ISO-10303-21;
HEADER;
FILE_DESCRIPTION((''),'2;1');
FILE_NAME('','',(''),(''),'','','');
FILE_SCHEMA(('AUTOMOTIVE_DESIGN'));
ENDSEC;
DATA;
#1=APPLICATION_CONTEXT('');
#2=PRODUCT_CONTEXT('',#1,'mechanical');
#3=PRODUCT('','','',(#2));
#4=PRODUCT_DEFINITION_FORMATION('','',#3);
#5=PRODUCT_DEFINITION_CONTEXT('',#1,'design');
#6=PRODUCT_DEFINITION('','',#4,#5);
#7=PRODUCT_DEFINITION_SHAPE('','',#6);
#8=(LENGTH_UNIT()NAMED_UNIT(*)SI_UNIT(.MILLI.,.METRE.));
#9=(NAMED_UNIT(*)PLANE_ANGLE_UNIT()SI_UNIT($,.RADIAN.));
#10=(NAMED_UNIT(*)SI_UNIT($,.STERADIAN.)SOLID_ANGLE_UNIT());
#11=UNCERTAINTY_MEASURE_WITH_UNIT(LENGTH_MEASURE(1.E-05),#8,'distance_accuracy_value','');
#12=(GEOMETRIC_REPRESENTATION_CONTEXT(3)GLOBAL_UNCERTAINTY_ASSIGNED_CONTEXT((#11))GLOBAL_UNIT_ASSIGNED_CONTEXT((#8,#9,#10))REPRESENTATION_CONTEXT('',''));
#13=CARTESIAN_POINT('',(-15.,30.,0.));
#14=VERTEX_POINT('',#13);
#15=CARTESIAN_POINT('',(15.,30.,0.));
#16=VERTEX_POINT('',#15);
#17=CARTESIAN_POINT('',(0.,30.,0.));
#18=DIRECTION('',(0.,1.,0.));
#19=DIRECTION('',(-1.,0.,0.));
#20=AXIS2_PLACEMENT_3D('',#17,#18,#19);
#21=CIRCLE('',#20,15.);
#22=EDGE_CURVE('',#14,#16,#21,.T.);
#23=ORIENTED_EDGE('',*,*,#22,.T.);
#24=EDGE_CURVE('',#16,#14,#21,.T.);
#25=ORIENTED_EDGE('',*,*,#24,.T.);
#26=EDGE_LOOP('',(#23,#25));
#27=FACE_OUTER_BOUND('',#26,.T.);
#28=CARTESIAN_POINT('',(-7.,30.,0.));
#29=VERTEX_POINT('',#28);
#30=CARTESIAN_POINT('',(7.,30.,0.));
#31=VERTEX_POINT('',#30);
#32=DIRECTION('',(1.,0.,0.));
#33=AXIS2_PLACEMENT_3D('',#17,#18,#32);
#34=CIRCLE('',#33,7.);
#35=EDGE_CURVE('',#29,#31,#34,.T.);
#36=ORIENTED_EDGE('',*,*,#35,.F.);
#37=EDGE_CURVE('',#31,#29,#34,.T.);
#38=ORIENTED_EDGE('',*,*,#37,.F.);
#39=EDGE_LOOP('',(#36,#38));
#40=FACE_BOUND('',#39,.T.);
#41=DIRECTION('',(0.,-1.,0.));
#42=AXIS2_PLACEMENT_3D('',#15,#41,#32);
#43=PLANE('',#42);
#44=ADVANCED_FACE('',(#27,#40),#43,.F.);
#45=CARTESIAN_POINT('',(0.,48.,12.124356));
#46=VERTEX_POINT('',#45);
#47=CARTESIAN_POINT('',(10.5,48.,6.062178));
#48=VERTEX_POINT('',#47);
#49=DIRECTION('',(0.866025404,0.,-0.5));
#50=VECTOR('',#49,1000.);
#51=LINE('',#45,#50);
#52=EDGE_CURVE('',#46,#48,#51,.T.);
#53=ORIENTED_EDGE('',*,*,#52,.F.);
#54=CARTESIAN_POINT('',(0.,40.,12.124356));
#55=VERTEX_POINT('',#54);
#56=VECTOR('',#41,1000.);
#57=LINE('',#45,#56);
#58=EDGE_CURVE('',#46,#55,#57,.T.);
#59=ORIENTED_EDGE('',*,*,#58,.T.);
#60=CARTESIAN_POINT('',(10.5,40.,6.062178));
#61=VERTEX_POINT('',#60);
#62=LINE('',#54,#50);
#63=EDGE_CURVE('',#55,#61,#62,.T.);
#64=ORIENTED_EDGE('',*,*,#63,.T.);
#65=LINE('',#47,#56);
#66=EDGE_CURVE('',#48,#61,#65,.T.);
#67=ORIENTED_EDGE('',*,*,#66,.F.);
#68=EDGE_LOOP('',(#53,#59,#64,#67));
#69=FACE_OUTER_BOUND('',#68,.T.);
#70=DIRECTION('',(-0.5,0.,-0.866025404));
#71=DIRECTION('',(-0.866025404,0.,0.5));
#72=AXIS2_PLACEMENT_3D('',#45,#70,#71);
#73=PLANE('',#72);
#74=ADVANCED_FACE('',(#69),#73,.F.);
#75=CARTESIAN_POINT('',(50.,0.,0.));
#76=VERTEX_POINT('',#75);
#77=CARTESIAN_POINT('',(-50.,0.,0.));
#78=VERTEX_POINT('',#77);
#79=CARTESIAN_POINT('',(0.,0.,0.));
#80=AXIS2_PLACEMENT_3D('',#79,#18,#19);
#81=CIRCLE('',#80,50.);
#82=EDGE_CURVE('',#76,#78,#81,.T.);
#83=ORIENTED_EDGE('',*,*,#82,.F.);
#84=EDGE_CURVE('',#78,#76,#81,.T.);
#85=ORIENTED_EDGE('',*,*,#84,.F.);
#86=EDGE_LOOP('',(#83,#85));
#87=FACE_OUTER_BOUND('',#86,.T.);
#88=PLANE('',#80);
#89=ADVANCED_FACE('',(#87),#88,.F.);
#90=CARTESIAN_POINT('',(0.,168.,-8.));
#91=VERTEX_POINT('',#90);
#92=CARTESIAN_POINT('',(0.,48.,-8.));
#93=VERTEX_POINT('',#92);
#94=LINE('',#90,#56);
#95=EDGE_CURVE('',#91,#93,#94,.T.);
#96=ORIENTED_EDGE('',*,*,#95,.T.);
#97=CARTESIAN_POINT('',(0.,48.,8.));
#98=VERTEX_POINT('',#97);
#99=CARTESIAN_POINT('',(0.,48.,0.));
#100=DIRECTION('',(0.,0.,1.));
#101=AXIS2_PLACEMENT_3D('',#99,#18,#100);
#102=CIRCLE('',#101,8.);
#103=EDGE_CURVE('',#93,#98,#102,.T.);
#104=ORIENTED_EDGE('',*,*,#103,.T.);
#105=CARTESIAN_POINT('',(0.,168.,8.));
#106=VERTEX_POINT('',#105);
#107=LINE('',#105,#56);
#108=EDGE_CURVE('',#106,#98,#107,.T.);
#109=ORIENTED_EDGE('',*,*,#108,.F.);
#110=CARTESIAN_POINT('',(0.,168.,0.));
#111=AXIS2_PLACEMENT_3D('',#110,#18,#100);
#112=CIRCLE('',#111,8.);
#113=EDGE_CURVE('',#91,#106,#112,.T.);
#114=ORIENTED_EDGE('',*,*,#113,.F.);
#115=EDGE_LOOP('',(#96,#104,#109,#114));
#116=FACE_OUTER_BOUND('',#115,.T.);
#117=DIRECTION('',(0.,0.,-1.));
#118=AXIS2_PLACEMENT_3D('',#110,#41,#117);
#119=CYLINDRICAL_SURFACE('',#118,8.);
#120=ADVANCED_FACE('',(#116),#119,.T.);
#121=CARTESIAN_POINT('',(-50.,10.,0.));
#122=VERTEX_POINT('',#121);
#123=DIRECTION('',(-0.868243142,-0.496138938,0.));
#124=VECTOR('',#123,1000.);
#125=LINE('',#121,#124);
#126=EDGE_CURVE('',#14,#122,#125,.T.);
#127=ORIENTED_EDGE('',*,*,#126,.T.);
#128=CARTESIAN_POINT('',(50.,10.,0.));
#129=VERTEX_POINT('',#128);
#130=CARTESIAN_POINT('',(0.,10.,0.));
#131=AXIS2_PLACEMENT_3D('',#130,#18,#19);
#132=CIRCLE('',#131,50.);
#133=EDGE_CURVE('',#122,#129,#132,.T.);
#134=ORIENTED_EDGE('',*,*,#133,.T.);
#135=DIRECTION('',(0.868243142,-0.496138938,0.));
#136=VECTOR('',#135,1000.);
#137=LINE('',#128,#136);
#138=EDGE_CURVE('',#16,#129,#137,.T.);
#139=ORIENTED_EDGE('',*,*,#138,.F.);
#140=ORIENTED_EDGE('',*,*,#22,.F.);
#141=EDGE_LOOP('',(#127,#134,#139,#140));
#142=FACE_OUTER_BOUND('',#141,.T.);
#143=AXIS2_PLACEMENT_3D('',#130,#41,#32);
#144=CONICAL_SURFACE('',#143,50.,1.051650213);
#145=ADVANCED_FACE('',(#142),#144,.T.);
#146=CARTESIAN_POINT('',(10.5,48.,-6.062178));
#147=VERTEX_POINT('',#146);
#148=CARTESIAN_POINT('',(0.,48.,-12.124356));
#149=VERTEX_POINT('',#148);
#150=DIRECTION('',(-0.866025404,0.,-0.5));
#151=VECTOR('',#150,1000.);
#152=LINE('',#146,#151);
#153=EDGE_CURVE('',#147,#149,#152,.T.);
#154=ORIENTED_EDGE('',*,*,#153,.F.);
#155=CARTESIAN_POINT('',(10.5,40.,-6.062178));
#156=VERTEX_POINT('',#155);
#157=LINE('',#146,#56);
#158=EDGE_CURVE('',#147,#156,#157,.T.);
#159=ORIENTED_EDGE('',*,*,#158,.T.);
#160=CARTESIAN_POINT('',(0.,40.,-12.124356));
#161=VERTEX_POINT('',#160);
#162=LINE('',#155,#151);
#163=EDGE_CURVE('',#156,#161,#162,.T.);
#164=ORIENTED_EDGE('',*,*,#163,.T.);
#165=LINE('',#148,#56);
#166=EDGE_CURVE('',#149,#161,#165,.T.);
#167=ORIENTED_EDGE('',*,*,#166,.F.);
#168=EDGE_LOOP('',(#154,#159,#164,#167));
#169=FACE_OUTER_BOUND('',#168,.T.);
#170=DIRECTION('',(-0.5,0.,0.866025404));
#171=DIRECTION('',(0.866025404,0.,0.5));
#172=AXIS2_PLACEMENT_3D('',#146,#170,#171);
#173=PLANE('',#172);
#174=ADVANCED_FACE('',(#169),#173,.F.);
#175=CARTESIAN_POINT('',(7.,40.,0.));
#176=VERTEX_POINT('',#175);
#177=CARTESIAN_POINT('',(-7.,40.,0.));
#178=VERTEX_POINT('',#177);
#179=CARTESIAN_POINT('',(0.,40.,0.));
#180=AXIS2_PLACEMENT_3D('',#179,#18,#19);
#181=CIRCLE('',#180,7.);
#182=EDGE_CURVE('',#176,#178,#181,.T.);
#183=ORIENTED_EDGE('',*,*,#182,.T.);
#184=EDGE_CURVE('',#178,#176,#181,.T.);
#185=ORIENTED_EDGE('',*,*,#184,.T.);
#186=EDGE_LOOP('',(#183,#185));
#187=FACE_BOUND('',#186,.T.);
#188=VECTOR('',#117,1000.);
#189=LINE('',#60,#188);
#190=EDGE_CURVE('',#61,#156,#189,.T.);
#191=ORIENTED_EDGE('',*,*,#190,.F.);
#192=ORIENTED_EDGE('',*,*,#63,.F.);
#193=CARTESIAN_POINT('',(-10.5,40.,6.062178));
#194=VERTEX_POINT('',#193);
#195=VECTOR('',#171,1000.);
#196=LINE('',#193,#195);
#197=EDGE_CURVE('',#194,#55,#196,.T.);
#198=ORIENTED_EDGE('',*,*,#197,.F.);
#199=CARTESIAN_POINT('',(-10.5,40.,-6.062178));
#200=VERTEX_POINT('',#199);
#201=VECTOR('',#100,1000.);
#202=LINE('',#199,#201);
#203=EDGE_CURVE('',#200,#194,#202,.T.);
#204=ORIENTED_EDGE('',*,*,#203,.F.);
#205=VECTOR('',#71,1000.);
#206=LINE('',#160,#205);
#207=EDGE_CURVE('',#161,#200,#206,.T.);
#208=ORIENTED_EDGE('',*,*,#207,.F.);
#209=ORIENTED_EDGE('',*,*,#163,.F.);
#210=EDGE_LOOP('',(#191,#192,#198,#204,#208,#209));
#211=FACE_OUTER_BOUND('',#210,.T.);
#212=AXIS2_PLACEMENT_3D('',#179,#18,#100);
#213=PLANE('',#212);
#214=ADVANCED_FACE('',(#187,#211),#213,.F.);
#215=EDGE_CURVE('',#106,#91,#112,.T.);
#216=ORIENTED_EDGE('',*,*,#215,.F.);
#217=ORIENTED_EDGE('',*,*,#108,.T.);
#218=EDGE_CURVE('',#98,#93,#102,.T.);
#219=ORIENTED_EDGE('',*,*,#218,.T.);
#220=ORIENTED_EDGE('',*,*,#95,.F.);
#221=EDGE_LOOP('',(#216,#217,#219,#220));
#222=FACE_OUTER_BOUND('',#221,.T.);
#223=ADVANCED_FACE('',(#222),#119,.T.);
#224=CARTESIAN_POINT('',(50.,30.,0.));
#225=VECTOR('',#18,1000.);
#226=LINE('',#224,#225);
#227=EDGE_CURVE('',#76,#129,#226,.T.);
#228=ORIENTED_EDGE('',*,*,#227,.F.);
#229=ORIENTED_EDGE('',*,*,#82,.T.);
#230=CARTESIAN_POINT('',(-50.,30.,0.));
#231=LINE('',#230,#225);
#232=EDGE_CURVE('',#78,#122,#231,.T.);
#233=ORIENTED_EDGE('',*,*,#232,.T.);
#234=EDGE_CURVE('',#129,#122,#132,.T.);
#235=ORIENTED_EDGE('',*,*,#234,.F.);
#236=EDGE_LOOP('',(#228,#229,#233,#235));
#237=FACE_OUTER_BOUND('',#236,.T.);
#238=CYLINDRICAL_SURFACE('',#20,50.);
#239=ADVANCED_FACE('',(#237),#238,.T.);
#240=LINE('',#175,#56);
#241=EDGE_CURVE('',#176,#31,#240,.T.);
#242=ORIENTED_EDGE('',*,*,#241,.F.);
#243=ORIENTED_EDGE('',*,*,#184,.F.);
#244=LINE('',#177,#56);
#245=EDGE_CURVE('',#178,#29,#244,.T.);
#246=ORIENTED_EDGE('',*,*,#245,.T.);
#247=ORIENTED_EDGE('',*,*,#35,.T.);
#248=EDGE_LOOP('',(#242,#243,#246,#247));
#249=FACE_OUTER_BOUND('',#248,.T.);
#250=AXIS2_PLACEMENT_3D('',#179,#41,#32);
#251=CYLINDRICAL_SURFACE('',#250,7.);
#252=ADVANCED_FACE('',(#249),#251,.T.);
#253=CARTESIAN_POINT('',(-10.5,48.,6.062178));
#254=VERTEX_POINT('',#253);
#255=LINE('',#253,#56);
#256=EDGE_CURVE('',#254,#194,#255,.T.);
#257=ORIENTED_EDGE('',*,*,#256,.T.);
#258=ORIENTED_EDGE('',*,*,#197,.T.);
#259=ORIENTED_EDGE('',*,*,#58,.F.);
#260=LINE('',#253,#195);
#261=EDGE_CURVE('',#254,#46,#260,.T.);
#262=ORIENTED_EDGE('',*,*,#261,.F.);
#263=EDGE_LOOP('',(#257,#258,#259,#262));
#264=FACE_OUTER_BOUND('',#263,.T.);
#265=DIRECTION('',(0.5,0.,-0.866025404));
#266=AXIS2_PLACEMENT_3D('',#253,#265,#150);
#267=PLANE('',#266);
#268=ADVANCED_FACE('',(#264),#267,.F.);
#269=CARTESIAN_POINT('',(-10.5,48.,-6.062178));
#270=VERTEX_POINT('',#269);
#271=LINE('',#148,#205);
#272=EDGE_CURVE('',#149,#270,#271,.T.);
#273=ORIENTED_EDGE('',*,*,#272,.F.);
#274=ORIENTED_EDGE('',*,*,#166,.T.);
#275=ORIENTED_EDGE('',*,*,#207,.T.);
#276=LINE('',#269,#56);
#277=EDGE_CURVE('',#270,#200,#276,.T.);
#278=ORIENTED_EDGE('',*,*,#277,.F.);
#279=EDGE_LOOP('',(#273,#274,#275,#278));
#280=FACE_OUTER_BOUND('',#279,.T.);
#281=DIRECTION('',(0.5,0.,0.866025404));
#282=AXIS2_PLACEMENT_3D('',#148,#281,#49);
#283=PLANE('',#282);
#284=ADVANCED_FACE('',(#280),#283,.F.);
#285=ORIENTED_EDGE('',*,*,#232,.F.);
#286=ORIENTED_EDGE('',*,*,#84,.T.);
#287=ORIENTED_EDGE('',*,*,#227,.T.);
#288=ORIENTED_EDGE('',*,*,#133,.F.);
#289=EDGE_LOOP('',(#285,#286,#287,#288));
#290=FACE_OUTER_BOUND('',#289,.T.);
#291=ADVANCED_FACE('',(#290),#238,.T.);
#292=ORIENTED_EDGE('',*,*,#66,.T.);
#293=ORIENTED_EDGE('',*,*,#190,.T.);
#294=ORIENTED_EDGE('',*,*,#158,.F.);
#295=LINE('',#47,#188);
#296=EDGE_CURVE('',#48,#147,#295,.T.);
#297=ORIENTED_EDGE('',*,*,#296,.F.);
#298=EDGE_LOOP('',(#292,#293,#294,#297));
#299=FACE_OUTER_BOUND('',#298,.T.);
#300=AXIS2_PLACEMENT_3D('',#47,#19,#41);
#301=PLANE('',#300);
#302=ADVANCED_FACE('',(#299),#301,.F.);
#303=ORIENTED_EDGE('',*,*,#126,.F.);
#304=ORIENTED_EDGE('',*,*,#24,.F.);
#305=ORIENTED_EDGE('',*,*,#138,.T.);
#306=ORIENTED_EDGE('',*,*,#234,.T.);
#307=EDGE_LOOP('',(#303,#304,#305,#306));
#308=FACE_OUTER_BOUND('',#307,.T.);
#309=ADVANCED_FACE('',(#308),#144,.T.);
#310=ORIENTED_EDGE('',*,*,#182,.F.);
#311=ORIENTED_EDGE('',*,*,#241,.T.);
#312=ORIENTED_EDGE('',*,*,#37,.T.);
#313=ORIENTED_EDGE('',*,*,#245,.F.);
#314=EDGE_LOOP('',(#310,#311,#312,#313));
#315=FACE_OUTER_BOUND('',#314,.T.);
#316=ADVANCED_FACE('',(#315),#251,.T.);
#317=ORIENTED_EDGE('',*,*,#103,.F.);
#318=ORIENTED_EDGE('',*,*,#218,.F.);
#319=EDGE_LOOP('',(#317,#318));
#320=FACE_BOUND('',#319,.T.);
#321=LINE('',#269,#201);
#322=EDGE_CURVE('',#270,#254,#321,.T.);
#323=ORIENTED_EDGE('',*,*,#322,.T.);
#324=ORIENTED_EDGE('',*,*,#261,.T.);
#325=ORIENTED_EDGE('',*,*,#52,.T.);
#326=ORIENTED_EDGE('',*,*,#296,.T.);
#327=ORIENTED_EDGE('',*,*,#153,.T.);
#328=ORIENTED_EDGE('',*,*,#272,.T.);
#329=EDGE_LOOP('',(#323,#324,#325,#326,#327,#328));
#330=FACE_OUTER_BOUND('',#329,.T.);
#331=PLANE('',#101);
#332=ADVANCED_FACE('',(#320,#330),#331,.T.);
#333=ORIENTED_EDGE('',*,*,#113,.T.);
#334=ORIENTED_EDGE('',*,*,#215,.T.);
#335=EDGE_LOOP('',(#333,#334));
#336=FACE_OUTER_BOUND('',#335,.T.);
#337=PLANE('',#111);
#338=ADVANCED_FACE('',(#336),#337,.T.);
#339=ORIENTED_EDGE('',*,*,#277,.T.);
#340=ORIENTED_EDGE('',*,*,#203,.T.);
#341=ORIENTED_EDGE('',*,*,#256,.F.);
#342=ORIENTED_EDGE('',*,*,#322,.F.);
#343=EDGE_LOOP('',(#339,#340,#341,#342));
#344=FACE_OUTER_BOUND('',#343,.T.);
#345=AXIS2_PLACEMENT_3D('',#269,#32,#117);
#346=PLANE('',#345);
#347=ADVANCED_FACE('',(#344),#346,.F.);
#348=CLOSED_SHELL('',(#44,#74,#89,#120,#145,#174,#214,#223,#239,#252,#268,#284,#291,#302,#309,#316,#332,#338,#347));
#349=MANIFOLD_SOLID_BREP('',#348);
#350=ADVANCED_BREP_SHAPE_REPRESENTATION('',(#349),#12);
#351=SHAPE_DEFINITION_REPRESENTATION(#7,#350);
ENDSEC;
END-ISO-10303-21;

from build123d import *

# Parameters (mm, degrees)
SKETCH_2_R      = 7
EXTRUDE_1_DEPTH = 10
EXTRUDE_2_DEPTH = 8
SKETCH_4_R      = 8
EXTRUDE_3_DEPTH = 120


with BuildPart() as part:
    # 草图1 → 旋转1 (revolve)
    with BuildSketch(Plane.XY, mode=Mode.PRIVATE) as revolve_1_sk:
        Polygon((0, 30), (0, 0), (50, 0), (50, 10), (15, 30), align=None)
    revolve(revolve_1_sk.sketch.rotate(Axis((0, 30, 0), (0, -1, 0)), 180), axis=Axis((0, 30, 0), (0, -1, 0)))

    # 草图2 → 凸台-拉伸1 (add)
    with BuildSketch(Plane(origin=(0, 30, 0), x_dir=(1, 0, 0), z_dir=(0, 1, 0))):
        Circle(SKETCH_2_R)
    extrude(amount=EXTRUDE_1_DEPTH)

    # 草图3 → 凸台-拉伸2 (add)
    with BuildSketch(Plane(origin=(0, 40, 0), x_dir=(1, 0, 0), z_dir=(0, 1, 0))):
        Polygon((0, 12.124355653), (-10.5, 6.062177826), (-10.5, -6.062177826), (0, -12.124355653), (10.5, -6.062177826), (10.5, 6.062177826), align=None)
    extrude(amount=EXTRUDE_2_DEPTH)

    # 草图4 → 凸台-拉伸3 (add)
    with BuildSketch(Plane(origin=(0, 48, 0), x_dir=(1, 0, 0), z_dir=(0, 1, 0))):
        with Locations(Location((0, 0, 0), (0, 0, 270))):
            Circle(SKETCH_4_R)
    extrude(amount=EXTRUDE_3_DEPTH)


solid = part.part
